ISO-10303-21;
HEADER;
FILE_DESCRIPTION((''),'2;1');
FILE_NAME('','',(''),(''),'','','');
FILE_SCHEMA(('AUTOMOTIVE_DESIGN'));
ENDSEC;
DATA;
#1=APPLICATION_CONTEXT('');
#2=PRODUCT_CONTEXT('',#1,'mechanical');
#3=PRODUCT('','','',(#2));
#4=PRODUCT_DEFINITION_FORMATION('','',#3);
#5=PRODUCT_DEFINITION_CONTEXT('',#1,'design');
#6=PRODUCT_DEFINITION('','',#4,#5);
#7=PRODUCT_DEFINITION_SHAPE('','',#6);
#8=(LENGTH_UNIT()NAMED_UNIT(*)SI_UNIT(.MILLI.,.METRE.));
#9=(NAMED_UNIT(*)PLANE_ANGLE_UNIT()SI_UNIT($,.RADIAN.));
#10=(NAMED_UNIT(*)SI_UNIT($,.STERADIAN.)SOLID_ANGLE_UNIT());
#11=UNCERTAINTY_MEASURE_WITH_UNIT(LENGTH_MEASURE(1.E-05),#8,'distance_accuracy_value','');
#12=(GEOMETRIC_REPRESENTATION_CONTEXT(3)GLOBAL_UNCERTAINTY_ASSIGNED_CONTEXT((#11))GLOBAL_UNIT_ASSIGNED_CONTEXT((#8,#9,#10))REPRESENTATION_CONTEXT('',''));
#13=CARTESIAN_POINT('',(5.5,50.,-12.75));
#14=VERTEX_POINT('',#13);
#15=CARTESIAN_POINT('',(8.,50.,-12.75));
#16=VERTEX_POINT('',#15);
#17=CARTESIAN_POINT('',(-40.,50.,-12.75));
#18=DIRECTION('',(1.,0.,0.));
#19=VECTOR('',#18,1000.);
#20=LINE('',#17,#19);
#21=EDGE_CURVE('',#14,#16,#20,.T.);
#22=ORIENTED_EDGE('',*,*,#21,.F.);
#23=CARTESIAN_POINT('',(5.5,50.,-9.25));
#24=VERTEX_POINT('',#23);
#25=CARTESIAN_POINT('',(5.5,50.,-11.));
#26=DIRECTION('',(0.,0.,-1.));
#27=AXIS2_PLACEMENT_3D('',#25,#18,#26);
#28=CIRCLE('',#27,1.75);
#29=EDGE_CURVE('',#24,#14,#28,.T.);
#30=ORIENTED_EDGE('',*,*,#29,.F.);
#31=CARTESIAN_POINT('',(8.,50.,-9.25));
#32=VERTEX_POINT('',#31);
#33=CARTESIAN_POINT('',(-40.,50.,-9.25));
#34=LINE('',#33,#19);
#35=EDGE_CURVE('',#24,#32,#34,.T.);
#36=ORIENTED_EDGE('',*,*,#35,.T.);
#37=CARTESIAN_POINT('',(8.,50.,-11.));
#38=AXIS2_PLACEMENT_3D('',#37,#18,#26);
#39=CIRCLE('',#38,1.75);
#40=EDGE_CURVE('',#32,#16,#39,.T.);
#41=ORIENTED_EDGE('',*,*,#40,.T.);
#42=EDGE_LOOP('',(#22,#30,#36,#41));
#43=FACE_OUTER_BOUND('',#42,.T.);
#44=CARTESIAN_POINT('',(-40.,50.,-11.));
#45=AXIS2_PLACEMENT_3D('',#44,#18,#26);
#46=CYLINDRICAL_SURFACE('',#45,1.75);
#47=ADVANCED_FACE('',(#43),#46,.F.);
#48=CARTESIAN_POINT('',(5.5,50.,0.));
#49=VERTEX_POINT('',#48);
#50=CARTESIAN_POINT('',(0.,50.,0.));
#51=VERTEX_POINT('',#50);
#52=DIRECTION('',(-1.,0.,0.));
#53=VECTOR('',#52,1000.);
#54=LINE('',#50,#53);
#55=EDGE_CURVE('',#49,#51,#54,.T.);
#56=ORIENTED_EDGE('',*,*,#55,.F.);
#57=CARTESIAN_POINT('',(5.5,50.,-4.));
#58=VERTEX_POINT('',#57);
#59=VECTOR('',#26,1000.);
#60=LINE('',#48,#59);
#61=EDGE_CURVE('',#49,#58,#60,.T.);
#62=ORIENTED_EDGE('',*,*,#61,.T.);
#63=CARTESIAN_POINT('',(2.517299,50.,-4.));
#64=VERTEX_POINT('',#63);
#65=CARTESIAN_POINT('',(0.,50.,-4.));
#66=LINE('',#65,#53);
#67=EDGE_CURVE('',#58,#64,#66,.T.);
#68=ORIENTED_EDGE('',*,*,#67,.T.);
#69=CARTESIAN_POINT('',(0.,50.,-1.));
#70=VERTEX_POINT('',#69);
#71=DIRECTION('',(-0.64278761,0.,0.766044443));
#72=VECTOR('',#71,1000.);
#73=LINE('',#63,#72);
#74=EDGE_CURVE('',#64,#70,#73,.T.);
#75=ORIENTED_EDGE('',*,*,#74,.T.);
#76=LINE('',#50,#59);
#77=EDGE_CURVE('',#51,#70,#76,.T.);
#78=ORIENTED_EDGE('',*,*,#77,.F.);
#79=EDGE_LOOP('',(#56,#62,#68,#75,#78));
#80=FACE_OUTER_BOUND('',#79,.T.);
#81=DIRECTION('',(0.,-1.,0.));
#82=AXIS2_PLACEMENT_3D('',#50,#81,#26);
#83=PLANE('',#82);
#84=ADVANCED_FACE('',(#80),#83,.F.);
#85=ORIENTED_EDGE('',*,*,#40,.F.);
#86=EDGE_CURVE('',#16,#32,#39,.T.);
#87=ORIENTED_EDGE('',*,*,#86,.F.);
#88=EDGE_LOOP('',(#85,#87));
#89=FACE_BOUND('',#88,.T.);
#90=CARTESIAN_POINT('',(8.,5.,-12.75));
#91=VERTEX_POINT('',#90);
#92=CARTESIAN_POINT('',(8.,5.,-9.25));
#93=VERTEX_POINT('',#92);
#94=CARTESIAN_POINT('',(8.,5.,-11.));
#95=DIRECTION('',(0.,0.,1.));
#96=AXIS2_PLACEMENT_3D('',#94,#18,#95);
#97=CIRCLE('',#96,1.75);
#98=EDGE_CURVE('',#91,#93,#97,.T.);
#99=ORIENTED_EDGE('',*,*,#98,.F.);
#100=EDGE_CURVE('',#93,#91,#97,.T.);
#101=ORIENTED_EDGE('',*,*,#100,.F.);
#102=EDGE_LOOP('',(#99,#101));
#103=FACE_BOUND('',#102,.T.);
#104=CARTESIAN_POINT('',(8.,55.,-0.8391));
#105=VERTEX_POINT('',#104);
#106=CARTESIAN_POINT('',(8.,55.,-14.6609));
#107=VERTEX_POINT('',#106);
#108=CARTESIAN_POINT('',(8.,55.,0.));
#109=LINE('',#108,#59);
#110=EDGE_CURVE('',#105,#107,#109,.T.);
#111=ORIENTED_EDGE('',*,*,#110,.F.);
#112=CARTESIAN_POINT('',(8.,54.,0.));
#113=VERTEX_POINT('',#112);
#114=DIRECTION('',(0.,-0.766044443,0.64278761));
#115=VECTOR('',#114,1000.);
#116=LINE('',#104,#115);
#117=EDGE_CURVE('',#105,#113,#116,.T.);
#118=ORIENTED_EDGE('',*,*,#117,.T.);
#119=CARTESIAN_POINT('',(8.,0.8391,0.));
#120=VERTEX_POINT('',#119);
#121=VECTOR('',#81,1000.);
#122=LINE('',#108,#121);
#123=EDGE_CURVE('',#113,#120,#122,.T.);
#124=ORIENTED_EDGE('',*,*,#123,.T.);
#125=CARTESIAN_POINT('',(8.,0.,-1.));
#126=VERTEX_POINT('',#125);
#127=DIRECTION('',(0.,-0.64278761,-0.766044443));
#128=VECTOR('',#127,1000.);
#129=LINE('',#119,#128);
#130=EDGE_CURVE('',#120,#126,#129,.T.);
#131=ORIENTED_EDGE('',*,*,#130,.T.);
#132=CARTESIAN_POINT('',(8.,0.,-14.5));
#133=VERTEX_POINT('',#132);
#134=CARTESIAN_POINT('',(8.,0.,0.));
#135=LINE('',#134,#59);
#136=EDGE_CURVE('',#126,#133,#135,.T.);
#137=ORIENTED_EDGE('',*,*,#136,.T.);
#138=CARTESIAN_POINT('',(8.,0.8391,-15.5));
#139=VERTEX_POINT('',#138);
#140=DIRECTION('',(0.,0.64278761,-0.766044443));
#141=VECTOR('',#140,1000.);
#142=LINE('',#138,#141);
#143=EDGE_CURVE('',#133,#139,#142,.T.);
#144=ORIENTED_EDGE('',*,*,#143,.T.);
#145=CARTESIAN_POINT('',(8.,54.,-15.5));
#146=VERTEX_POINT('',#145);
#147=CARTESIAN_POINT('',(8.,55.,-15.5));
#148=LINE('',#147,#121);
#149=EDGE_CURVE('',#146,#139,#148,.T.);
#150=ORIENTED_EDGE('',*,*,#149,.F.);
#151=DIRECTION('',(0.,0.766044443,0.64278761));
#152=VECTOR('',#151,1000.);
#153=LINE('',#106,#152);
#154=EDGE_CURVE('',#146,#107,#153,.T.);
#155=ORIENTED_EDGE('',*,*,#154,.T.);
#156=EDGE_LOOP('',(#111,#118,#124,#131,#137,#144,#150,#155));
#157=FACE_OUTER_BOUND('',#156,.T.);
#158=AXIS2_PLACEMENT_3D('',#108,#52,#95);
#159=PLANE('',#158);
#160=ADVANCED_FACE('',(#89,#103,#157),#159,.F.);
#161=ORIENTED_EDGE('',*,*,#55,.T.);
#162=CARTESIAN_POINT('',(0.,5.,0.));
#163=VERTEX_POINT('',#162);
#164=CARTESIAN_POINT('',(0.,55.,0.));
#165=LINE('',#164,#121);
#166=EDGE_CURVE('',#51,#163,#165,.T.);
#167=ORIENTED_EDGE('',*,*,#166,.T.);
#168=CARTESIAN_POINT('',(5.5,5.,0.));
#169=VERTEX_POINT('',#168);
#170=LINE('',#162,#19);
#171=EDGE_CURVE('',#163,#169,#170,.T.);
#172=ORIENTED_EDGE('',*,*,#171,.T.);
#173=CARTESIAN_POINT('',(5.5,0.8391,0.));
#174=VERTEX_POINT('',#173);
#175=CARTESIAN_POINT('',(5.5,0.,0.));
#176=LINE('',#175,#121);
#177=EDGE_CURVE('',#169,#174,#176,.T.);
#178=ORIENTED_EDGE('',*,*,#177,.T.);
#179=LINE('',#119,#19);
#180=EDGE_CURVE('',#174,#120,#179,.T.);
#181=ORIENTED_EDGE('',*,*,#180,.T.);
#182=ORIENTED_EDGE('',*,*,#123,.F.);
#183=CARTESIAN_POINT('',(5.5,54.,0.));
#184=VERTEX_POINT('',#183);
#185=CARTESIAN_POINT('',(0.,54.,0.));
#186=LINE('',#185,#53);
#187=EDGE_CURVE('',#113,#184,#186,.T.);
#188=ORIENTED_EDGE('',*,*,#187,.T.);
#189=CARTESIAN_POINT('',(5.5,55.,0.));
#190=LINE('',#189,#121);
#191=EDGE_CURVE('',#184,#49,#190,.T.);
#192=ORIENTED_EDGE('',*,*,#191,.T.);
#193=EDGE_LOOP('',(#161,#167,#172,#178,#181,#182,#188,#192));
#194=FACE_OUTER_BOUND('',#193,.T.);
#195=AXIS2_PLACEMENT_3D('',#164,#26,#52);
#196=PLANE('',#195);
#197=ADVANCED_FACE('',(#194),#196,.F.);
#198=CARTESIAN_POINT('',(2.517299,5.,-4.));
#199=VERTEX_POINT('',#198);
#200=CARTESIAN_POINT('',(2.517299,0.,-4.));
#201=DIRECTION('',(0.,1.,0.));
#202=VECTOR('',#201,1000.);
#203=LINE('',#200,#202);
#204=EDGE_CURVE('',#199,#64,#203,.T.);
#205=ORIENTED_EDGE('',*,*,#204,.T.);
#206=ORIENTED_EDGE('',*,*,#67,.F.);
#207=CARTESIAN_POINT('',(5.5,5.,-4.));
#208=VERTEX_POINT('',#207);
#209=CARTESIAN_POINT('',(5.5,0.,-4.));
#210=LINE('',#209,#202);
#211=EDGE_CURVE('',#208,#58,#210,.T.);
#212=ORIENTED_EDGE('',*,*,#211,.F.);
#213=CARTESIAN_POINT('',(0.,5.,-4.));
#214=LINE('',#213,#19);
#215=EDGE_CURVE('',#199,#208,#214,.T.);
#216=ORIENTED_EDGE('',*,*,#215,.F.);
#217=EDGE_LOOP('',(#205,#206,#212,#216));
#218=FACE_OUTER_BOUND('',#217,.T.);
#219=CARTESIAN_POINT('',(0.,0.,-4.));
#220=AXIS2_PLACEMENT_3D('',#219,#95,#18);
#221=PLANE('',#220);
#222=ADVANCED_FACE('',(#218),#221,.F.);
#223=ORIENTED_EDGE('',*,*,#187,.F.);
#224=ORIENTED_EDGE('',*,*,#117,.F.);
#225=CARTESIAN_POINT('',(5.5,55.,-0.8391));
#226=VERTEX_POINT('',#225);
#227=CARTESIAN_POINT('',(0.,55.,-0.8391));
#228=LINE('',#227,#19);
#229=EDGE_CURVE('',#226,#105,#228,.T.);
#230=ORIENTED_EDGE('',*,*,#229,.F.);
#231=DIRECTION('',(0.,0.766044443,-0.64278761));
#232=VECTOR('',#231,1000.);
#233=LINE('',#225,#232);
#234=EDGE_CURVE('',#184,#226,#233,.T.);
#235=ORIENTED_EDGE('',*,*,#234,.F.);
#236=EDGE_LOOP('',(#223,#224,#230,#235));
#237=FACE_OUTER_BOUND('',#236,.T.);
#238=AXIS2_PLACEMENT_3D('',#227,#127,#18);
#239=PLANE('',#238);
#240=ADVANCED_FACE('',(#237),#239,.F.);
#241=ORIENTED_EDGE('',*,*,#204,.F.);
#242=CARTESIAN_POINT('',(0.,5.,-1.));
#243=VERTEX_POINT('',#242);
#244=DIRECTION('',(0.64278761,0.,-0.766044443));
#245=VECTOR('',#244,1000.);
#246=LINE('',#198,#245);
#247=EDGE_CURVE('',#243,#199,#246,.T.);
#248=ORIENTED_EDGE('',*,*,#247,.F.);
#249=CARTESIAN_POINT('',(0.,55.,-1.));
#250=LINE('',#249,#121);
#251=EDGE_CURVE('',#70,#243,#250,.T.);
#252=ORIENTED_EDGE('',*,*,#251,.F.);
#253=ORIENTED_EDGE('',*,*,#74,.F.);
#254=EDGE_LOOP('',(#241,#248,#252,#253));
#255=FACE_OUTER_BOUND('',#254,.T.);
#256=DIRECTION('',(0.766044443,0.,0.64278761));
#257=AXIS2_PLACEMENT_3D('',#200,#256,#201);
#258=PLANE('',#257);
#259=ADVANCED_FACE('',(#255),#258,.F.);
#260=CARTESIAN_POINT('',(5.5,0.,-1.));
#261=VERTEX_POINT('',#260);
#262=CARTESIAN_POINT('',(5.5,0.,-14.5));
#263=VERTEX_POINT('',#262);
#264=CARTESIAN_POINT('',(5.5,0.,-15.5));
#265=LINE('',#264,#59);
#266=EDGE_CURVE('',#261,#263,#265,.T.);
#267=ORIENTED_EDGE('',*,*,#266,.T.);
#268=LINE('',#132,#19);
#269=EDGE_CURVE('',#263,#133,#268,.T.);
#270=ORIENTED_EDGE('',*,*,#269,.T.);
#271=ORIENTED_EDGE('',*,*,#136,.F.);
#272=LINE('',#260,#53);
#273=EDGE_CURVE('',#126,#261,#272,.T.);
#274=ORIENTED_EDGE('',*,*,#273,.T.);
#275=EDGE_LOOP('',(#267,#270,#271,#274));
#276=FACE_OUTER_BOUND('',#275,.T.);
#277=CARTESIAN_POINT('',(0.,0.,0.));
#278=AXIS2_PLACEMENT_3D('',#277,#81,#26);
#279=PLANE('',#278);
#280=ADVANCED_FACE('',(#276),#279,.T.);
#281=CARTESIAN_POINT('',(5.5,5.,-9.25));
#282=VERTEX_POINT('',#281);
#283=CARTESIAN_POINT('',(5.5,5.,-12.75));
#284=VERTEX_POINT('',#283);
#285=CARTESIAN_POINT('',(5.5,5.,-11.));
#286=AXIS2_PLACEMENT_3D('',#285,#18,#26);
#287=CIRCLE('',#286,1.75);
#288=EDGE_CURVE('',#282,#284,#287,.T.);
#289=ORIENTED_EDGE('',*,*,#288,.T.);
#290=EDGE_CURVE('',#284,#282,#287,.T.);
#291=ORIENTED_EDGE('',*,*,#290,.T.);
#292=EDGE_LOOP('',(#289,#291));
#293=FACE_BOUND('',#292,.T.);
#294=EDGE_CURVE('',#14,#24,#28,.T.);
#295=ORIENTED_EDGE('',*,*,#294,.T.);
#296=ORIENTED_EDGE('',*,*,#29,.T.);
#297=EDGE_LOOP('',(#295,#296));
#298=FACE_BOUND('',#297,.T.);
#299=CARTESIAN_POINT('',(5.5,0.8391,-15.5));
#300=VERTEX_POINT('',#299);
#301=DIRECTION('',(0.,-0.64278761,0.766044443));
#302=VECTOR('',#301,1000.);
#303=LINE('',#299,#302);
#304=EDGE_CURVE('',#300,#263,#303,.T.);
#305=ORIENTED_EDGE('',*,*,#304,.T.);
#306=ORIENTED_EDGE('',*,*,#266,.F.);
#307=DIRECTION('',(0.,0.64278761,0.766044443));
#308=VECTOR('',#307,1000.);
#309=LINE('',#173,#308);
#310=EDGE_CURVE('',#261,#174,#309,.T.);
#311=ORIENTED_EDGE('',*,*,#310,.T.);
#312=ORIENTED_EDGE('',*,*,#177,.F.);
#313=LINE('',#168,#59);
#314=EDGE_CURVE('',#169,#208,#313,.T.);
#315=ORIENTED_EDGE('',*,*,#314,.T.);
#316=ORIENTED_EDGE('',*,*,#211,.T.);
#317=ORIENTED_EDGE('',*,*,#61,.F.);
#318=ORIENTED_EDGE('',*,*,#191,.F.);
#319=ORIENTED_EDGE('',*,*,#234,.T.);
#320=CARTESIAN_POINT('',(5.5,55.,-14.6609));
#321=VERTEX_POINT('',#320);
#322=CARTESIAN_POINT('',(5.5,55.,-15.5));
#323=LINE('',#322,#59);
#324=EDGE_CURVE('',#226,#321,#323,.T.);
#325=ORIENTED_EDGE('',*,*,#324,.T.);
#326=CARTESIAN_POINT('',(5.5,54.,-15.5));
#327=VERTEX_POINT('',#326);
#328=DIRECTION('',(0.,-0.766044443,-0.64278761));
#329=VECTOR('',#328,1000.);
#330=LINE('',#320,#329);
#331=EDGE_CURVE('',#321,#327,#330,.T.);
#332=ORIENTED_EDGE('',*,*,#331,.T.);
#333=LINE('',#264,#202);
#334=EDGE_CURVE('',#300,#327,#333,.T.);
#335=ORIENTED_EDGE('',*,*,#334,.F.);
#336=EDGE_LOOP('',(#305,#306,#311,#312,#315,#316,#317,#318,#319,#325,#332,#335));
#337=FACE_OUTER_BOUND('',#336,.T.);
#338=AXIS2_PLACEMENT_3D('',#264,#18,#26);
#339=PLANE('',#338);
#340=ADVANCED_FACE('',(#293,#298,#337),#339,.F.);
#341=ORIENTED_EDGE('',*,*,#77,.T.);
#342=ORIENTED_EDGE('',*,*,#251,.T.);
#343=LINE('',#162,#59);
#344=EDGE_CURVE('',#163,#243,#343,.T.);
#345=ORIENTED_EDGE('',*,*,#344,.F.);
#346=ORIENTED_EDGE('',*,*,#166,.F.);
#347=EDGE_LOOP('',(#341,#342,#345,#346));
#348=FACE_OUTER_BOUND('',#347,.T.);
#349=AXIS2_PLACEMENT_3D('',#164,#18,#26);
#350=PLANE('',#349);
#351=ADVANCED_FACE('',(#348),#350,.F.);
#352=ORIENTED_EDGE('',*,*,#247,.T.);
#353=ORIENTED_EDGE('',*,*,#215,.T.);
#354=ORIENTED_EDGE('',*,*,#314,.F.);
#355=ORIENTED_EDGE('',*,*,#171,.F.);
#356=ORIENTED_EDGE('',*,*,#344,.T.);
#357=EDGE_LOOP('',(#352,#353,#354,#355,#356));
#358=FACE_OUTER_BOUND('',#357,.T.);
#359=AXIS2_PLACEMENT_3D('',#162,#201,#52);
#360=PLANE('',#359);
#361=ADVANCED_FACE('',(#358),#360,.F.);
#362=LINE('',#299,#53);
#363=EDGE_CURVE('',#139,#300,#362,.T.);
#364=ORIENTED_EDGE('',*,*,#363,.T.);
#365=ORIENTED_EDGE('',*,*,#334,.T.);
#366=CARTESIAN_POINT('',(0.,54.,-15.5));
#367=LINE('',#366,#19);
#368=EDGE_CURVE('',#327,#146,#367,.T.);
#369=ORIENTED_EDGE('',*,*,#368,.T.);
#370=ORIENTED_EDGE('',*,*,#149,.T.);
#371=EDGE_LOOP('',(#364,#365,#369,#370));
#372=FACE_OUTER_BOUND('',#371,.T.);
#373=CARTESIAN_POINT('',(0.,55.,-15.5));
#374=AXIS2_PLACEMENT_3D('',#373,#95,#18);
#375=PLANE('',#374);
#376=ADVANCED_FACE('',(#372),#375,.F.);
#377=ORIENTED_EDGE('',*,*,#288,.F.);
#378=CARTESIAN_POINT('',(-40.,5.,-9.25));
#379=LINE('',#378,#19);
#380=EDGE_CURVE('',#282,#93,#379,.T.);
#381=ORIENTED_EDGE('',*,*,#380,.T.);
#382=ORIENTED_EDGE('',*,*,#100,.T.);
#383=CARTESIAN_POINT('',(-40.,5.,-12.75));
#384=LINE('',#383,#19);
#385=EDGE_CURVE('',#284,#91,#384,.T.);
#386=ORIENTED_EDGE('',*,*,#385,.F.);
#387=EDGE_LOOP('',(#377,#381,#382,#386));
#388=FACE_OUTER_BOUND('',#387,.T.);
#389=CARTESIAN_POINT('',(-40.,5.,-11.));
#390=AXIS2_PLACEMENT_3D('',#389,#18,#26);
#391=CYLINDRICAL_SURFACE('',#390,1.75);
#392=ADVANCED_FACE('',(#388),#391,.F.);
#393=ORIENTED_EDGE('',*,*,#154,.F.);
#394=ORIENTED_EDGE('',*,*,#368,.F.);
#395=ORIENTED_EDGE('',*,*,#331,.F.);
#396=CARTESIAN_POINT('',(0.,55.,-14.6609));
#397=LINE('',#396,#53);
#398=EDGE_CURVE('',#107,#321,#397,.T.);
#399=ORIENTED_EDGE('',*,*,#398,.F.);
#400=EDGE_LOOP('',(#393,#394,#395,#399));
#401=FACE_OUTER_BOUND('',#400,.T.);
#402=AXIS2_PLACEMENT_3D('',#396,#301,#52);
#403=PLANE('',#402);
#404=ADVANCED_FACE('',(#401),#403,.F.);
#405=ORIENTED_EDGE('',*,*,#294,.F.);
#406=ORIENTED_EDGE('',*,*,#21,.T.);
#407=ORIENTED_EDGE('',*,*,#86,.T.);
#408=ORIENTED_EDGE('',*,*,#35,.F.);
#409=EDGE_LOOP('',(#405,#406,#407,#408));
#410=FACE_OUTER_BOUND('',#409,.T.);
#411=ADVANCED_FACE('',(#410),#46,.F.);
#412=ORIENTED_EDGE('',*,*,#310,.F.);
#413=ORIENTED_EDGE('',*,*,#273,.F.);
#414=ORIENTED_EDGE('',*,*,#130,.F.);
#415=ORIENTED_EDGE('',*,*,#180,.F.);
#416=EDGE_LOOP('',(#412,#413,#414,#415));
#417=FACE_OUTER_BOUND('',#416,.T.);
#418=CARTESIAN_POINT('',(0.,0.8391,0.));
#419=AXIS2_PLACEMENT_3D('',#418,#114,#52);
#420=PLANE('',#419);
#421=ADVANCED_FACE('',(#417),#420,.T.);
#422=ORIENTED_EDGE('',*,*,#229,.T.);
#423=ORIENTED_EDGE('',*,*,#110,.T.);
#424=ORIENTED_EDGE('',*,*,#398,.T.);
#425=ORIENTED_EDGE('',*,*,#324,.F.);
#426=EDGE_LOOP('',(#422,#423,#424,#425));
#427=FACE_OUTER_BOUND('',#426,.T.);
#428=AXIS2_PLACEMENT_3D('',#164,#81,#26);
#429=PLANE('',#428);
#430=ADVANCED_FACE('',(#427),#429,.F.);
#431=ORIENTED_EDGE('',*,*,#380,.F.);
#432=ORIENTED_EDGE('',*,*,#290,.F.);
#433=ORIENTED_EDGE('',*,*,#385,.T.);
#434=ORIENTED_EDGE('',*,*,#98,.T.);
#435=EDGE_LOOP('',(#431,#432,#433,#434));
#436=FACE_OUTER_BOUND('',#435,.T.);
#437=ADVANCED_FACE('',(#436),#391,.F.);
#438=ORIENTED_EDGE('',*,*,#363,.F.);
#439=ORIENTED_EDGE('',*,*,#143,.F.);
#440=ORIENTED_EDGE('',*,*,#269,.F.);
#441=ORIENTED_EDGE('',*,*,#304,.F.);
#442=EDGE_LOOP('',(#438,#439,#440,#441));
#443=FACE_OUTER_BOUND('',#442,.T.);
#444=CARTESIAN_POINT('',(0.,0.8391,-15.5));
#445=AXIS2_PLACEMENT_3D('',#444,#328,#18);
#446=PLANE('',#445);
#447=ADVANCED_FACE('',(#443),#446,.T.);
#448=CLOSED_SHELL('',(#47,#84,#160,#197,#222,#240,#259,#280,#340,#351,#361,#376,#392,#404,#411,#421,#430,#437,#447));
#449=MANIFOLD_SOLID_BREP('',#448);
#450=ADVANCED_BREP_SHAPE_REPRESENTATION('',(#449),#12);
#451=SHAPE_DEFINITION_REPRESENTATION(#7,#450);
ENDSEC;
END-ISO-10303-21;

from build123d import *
from OCP.BRepFilletAPI import BRepFilletAPI_MakeChamfer

# Parameters (mm, degrees)
SKETCH1_W           = 8
SKETCH1_H           = 15.5
BOSS_EXTRUDE1_DEPTH = 55
SKETCH2_W           = 5.5
SKETCH2_H           = 11.5
CUT_EXTRUDE1_DEPTH  = 58.699653379
CHAMFER1_SIZE       = 3
CHAMFER1_SIZE2      = 2.517298894
SKETCH3_R           = 1.75
CUT_EXTRUDE2_DEPTH  = 48
SKETCH4_W           = 5.5
SKETCH4_H           = 5
CUT_EXTRUDE3_DEPTH  = 57.756056945
CHAMFER2_SIZE       = 1
CHAMFER2_SIZE2      = 0.839099631


with BuildPart() as part:
    # Sketch1 → Boss-Extrude1 (new body)
    with BuildSketch(Plane(origin=(0, 0, 0), x_dir=(1, 0, 0), z_dir=(0, 1, 0))):
        with Locations((4, 7.75)):
            Rectangle(SKETCH1_W, SKETCH1_H)
    extrude(amount=BOSS_EXTRUDE1_DEPTH)

    # Sketch2 → Cut-Extrude1 (cut, through all)
    with BuildSketch(Plane(origin=(0, 55, 0), x_dir=(1, 0, 0), z_dir=(0, 1, 0))):
        with Locations((2.75, 9.75)):
            Rectangle(SKETCH2_W, SKETCH2_H)
    extrude(amount=-CUT_EXTRUDE1_DEPTH, mode=Mode.SUBTRACT)

    # Chamfer1
    chamfer1_edges = [part.edges().sort_by_distance(p)[0] for p in [
        (0, 27.5, -4),
    ]]
    chamfer1_side = [part.faces().sort_by_distance(p)[0] for p in [
        (0, 27.5, -2),
    ]]
    chamfer(chamfer1_edges, length=CHAMFER1_SIZE, length2=CHAMFER1_SIZE2, reference=chamfer1_side[0])

    # Sketch3 → Cut-Extrude2 (cut)
    with BuildSketch(Plane(origin=(8, 0, 0), x_dir=(0, 0, -1), z_dir=(1, 0, 0))):
        with Locations((11, 50)):
            Circle(SKETCH3_R)
        with Locations((11, 5)):
            Circle(SKETCH3_R)
    extrude(amount=-CUT_EXTRUDE2_DEPTH, mode=Mode.SUBTRACT)

    # Sketch4 → Cut-Extrude3 (cut, through all)
    with BuildSketch(Plane(origin=(0, 0, -4), x_dir=(-1, 0, 0), z_dir=(0, 0, -1))):
        with Locations((-2.75, 52.5)):
            Rectangle(SKETCH4_W, SKETCH4_H)
        with Locations((-2.75, 2.5)):
            Rectangle(SKETCH4_W, SKETCH4_H)
    extrude(amount=-CUT_EXTRUDE3_DEPTH, mode=Mode.SUBTRACT)

    # Chamfer2: one chamfer whose edges measure the first distance from different faces: ONE call of the kernel's chamfer builder (chamfer() names one face for all edges)
    chamfer2_edges_1 = [part.edges().sort_by_distance(p)[0] for p in [
        (6.75, 55, -15.5),
    ]]
    chamfer2_side_1 = [part.faces().sort_by_distance(p)[0] for p in [
        (6.75, 27.5, -15.5),
    ]]
    chamfer2_edges_2 = [part.edges().sort_by_distance(p)[0] for p in [
        (6.75, 0, -15.5),
        (6.75, 0, 0),
    ]]
    chamfer2_side_2 = [part.faces().sort_by_distance(p)[0] for p in [
        (6.75, 0, -7.75),
    ]]
    chamfer2_edges_3 = [part.edges().sort_by_distance(p)[0] for p in [
        (6.75, 55, 0),
    ]]
    chamfer2_side_3 = [part.faces().sort_by_distance(p)[0] for p in [
        (4.178571429, 27.5, 0),
    ]]
    chamfer2 = BRepFilletAPI_MakeChamfer(part.part.solid().wrapped)
    for e in chamfer2_edges_1:
        chamfer2.Add(CHAMFER2_SIZE, CHAMFER2_SIZE2, e.wrapped, chamfer2_side_1[0].wrapped)  # the first distance lies on this face
    for e in chamfer2_edges_2:
        chamfer2.Add(CHAMFER2_SIZE, CHAMFER2_SIZE2, e.wrapped, chamfer2_side_2[0].wrapped)  # the first distance lies on this face
    for e in chamfer2_edges_3:
        chamfer2.Add(CHAMFER2_SIZE, CHAMFER2_SIZE2, e.wrapped, chamfer2_side_3[0].wrapped)  # the first distance lies on this face
    add(Compound.cast(chamfer2.Shape()), mode=Mode.REPLACE)


solid = part.part
